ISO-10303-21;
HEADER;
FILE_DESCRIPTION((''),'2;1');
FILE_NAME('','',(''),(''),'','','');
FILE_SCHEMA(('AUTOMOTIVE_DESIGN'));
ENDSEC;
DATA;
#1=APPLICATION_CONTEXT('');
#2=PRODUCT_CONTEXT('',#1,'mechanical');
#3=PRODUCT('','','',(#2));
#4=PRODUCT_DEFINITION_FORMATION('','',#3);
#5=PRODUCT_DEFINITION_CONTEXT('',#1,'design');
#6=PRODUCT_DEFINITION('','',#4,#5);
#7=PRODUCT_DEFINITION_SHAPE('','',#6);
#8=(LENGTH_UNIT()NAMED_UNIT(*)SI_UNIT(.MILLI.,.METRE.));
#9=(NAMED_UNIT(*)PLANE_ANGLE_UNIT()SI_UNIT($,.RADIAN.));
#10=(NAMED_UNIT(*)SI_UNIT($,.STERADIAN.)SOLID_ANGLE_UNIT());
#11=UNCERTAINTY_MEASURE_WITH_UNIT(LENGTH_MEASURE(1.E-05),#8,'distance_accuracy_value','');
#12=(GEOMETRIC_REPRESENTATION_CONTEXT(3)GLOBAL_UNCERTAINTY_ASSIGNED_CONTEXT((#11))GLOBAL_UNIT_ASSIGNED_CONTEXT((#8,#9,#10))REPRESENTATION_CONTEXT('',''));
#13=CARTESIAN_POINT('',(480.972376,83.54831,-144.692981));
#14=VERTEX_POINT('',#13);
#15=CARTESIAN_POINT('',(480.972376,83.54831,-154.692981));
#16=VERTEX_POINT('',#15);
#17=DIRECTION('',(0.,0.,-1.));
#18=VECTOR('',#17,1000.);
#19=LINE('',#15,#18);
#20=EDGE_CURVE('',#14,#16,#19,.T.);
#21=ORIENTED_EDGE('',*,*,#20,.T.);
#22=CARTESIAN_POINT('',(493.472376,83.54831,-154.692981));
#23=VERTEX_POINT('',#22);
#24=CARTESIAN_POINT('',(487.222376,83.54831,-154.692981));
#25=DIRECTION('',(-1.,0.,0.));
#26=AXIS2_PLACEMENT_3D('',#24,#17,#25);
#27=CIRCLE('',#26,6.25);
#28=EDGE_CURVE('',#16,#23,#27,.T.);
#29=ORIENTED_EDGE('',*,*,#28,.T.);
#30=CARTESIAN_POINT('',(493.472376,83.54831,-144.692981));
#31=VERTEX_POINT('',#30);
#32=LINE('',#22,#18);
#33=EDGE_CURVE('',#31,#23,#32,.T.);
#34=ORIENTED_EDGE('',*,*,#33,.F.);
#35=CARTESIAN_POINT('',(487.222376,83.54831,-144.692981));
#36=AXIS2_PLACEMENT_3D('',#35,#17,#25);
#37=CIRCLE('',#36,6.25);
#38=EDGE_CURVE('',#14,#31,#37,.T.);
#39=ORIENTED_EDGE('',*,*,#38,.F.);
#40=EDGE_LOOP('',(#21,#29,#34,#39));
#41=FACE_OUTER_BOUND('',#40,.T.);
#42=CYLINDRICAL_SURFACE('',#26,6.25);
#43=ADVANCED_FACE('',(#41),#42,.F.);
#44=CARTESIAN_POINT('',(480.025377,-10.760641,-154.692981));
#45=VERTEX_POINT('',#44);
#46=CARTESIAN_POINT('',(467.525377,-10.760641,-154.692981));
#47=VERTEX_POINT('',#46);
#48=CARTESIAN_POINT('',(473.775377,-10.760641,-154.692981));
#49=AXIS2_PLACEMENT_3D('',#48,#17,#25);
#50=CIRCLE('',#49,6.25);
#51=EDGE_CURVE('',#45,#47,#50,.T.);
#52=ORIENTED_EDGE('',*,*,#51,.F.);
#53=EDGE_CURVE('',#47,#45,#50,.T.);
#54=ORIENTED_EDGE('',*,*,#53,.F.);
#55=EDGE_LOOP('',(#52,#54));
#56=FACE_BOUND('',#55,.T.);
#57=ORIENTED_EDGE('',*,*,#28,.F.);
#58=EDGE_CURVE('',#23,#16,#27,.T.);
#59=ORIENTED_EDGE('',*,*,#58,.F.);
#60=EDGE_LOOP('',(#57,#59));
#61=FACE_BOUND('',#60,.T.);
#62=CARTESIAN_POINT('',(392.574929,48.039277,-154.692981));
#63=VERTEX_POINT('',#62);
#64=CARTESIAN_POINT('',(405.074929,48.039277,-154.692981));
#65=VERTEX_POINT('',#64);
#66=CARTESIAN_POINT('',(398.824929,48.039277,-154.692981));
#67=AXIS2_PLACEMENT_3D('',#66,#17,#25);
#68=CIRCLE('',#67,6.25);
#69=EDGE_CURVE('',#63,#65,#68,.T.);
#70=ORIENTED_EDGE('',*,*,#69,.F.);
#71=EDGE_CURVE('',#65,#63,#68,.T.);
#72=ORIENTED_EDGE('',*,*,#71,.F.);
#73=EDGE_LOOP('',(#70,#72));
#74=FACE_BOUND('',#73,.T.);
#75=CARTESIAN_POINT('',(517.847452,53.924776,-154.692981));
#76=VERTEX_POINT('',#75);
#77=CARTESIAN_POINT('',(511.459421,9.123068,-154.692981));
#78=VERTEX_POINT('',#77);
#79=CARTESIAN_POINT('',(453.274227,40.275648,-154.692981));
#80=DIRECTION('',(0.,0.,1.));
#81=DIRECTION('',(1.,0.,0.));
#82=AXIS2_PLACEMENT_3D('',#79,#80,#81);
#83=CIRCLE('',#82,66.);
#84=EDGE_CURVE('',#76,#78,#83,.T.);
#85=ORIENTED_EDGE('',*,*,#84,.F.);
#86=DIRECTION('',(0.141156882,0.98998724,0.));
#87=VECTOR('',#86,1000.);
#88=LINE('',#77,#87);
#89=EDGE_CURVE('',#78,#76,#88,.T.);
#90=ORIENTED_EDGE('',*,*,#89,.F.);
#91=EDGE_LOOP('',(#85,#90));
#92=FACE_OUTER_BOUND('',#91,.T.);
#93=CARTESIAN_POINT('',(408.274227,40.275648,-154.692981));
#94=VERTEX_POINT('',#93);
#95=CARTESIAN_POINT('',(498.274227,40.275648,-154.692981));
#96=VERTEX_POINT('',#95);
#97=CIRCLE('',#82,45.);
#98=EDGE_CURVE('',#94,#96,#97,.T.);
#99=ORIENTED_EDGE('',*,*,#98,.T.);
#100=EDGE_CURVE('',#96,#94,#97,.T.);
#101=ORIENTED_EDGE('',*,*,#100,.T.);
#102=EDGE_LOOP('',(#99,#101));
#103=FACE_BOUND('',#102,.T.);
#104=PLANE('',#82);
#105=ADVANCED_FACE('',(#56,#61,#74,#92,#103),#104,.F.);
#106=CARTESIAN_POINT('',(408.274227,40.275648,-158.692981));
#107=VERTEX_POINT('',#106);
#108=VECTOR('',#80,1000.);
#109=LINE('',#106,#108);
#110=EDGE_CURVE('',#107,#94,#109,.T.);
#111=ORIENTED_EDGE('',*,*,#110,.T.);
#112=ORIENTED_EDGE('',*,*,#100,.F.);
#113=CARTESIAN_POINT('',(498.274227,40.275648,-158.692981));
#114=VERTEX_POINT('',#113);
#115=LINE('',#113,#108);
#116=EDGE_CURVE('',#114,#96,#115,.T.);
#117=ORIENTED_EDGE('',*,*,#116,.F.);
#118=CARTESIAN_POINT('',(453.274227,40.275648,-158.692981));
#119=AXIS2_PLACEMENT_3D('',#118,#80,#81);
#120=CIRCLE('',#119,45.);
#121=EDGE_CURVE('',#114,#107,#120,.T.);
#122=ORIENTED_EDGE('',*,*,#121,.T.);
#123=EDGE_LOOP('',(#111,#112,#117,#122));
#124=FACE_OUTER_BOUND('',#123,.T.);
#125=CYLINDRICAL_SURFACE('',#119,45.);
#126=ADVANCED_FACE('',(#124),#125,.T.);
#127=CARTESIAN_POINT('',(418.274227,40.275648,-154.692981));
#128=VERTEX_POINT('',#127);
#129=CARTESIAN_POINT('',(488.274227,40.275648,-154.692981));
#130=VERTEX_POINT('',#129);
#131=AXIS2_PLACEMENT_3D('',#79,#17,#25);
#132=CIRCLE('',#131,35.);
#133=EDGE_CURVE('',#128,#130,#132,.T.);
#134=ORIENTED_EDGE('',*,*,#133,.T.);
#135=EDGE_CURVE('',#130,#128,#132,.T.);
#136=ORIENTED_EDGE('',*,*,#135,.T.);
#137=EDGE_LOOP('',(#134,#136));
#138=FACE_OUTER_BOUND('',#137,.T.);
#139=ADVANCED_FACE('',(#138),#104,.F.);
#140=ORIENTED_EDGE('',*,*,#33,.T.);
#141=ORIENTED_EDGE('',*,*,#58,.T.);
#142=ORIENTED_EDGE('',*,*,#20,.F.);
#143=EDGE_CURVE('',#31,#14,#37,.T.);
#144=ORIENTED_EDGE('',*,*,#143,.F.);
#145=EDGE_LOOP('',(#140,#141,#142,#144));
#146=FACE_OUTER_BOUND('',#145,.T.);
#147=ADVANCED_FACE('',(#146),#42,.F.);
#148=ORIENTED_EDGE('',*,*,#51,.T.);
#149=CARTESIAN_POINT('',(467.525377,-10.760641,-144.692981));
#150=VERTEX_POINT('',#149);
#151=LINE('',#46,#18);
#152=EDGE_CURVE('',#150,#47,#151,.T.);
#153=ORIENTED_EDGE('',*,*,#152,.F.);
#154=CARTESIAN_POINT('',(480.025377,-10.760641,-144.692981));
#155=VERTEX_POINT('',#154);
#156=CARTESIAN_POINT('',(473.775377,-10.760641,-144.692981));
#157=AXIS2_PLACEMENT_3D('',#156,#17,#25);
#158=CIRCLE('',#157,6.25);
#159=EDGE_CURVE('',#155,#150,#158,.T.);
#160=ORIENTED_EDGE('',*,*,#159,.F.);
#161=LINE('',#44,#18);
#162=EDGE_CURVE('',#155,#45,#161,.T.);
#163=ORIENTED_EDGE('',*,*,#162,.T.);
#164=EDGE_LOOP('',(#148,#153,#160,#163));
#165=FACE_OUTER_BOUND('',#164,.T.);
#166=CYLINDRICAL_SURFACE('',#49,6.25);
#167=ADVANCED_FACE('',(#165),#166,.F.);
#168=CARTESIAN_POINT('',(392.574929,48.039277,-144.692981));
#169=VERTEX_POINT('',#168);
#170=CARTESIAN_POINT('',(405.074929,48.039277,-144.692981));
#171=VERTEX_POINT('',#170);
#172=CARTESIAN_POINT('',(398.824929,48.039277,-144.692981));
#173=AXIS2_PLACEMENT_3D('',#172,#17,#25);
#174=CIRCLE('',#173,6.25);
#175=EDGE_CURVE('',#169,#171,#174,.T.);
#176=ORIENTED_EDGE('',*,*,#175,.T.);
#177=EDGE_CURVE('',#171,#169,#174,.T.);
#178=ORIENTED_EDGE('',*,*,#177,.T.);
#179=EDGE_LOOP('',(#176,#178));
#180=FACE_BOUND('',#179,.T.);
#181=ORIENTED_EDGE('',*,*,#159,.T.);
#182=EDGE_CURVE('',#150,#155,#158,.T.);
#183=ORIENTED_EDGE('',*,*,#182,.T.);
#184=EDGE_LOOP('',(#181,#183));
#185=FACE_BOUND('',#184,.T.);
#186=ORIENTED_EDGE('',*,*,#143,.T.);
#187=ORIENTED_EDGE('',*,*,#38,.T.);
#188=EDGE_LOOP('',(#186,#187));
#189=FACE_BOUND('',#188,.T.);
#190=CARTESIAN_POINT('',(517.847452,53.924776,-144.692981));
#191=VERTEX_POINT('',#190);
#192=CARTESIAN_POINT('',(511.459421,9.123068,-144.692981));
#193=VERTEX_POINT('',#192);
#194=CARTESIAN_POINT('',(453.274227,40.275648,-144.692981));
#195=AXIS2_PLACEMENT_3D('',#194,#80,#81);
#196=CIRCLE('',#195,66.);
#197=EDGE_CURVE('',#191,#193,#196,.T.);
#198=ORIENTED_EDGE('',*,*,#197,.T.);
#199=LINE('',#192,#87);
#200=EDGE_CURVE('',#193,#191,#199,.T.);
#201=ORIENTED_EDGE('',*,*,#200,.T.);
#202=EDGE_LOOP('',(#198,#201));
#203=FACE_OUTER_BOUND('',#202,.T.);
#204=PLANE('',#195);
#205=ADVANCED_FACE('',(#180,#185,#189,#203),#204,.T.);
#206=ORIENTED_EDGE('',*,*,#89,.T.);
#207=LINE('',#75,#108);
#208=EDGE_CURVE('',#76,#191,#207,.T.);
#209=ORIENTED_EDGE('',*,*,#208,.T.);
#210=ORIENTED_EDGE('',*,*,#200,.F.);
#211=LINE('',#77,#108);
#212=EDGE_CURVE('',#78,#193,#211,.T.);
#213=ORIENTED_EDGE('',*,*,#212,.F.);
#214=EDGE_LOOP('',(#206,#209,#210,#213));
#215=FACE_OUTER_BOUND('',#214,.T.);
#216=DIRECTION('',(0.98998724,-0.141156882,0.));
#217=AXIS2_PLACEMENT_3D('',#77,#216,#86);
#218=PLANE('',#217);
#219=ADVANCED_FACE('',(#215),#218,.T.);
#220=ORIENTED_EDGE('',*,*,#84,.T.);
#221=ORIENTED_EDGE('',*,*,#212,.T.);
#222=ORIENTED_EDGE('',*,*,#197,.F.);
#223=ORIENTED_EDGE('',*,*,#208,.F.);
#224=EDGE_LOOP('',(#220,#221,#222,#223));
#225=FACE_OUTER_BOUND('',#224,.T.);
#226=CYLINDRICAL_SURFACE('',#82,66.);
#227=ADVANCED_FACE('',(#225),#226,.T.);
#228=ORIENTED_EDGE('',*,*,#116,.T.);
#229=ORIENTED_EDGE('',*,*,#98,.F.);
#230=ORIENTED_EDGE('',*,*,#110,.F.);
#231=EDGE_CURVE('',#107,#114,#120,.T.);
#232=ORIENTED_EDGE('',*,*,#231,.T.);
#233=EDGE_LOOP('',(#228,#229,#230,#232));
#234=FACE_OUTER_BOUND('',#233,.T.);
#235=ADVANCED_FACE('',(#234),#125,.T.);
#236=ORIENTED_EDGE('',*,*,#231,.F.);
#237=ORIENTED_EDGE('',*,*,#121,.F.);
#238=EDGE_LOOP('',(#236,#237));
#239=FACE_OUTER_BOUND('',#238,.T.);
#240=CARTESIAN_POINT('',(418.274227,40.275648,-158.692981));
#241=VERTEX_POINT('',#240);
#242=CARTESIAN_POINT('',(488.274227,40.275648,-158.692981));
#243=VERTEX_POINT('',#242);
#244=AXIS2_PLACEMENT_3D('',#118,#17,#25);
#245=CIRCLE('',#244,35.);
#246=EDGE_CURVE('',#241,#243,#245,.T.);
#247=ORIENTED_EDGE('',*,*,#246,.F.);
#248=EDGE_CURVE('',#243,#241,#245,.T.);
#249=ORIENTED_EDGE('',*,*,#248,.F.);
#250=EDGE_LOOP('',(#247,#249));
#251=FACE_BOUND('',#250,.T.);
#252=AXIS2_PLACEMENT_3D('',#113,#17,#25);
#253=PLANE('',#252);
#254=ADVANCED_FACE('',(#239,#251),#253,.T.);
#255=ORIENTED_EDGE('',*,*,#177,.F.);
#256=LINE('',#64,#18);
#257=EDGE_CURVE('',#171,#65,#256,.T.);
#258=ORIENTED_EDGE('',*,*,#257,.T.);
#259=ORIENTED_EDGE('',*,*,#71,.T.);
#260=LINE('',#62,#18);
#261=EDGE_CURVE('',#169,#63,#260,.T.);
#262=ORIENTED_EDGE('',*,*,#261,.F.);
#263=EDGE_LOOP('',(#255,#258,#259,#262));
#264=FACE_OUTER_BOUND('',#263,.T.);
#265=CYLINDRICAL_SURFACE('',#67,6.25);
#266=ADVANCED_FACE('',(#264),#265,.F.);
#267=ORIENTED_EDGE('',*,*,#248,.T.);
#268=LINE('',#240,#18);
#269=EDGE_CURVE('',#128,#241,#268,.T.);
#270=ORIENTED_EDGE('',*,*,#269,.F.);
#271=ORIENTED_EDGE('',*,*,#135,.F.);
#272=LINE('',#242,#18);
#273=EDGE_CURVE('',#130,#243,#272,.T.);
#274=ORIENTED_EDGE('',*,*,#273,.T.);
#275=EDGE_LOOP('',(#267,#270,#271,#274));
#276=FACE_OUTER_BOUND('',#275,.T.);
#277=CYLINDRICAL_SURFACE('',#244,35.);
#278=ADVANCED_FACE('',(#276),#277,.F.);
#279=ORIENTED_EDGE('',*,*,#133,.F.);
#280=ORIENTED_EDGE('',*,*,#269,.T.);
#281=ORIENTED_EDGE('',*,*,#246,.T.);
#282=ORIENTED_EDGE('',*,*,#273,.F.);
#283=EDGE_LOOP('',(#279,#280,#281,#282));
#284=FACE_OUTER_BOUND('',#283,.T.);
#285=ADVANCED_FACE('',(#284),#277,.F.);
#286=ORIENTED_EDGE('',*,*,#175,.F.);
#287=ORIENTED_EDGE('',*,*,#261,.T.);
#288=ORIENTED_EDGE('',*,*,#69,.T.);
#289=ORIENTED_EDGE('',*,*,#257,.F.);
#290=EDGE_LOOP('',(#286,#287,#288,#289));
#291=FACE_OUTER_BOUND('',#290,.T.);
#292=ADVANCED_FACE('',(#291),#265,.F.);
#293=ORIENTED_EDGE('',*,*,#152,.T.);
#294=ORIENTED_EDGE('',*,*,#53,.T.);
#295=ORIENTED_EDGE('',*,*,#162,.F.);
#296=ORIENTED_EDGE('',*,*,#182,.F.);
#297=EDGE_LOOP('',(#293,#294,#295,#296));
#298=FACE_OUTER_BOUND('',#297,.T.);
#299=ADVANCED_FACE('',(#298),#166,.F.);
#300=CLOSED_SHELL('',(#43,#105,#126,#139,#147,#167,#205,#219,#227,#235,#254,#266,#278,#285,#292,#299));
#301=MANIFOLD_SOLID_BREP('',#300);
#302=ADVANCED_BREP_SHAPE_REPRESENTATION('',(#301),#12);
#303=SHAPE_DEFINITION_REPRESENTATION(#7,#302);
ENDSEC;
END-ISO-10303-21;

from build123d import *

# Parameters (mm, degrees)
BOSS_EXTRUDE1_DEPTH          = 10
SKETCH2_W                    = 45
SKETCH2_H                    = 4
F_12_5_12_5_DIAMETER_HOLE1_D = 12.5
M64_CLEARANCE_HOLE1_D        = 70
M64_CLEARANCE_HOLE1_DEPTH    = 4


with BuildPart() as part:
    # Sketch1 → Boss-Extrude1 (new body)
    with BuildSketch(Plane.XY.offset(-144.692981355)):
        with BuildLine():
            Line((511.459420647, 9.123067621), (517.84745191, 53.924775809))
            ThreePointArc((517.84745191, 53.924775809), (387.935069604, 49.592002612), (511.459420647, 9.123067621))
        make_face()
    extrude(amount=-BOSS_EXTRUDE1_DEPTH)

    # Sketch2 → Revolve1 (revolve)
    with BuildSketch(Plane(origin=(0, 40.2756484, 0), x_dir=(1, 0, 0), z_dir=(0, 1, 0))):
        with Locations((475.77422742, 156.692981355)):
            Rectangle(SKETCH2_W, SKETCH2_H)
    revolve(axis=Axis((453.27422742, 40.2756484, -158.692981355), (0, 0, 1)))

    # Ø12.5 (12.5) Diameter Hole1 (through all)
    with Locations(Plane(origin=(0, 0, -154.692981355), x_dir=(-1, 0, 0), z_dir=(0, 0, -1))):
        with Locations((-398.82492924, 48.03927691), (-487.222376026, 83.548309587), (-473.775376995, -10.760641298)):
            Hole(F_12_5_12_5_DIAMETER_HOLE1_D / 2)

    # M64 Clearance Hole1
    with Locations(Plane(origin=(0, 0, -158.692981355), x_dir=(-1, 0, 0), z_dir=(0, 0, -1))):
        with Locations((-453.27422742, 40.2756484)):
            Hole(M64_CLEARANCE_HOLE1_D / 2, depth=M64_CLEARANCE_HOLE1_DEPTH)


solid = part.part
